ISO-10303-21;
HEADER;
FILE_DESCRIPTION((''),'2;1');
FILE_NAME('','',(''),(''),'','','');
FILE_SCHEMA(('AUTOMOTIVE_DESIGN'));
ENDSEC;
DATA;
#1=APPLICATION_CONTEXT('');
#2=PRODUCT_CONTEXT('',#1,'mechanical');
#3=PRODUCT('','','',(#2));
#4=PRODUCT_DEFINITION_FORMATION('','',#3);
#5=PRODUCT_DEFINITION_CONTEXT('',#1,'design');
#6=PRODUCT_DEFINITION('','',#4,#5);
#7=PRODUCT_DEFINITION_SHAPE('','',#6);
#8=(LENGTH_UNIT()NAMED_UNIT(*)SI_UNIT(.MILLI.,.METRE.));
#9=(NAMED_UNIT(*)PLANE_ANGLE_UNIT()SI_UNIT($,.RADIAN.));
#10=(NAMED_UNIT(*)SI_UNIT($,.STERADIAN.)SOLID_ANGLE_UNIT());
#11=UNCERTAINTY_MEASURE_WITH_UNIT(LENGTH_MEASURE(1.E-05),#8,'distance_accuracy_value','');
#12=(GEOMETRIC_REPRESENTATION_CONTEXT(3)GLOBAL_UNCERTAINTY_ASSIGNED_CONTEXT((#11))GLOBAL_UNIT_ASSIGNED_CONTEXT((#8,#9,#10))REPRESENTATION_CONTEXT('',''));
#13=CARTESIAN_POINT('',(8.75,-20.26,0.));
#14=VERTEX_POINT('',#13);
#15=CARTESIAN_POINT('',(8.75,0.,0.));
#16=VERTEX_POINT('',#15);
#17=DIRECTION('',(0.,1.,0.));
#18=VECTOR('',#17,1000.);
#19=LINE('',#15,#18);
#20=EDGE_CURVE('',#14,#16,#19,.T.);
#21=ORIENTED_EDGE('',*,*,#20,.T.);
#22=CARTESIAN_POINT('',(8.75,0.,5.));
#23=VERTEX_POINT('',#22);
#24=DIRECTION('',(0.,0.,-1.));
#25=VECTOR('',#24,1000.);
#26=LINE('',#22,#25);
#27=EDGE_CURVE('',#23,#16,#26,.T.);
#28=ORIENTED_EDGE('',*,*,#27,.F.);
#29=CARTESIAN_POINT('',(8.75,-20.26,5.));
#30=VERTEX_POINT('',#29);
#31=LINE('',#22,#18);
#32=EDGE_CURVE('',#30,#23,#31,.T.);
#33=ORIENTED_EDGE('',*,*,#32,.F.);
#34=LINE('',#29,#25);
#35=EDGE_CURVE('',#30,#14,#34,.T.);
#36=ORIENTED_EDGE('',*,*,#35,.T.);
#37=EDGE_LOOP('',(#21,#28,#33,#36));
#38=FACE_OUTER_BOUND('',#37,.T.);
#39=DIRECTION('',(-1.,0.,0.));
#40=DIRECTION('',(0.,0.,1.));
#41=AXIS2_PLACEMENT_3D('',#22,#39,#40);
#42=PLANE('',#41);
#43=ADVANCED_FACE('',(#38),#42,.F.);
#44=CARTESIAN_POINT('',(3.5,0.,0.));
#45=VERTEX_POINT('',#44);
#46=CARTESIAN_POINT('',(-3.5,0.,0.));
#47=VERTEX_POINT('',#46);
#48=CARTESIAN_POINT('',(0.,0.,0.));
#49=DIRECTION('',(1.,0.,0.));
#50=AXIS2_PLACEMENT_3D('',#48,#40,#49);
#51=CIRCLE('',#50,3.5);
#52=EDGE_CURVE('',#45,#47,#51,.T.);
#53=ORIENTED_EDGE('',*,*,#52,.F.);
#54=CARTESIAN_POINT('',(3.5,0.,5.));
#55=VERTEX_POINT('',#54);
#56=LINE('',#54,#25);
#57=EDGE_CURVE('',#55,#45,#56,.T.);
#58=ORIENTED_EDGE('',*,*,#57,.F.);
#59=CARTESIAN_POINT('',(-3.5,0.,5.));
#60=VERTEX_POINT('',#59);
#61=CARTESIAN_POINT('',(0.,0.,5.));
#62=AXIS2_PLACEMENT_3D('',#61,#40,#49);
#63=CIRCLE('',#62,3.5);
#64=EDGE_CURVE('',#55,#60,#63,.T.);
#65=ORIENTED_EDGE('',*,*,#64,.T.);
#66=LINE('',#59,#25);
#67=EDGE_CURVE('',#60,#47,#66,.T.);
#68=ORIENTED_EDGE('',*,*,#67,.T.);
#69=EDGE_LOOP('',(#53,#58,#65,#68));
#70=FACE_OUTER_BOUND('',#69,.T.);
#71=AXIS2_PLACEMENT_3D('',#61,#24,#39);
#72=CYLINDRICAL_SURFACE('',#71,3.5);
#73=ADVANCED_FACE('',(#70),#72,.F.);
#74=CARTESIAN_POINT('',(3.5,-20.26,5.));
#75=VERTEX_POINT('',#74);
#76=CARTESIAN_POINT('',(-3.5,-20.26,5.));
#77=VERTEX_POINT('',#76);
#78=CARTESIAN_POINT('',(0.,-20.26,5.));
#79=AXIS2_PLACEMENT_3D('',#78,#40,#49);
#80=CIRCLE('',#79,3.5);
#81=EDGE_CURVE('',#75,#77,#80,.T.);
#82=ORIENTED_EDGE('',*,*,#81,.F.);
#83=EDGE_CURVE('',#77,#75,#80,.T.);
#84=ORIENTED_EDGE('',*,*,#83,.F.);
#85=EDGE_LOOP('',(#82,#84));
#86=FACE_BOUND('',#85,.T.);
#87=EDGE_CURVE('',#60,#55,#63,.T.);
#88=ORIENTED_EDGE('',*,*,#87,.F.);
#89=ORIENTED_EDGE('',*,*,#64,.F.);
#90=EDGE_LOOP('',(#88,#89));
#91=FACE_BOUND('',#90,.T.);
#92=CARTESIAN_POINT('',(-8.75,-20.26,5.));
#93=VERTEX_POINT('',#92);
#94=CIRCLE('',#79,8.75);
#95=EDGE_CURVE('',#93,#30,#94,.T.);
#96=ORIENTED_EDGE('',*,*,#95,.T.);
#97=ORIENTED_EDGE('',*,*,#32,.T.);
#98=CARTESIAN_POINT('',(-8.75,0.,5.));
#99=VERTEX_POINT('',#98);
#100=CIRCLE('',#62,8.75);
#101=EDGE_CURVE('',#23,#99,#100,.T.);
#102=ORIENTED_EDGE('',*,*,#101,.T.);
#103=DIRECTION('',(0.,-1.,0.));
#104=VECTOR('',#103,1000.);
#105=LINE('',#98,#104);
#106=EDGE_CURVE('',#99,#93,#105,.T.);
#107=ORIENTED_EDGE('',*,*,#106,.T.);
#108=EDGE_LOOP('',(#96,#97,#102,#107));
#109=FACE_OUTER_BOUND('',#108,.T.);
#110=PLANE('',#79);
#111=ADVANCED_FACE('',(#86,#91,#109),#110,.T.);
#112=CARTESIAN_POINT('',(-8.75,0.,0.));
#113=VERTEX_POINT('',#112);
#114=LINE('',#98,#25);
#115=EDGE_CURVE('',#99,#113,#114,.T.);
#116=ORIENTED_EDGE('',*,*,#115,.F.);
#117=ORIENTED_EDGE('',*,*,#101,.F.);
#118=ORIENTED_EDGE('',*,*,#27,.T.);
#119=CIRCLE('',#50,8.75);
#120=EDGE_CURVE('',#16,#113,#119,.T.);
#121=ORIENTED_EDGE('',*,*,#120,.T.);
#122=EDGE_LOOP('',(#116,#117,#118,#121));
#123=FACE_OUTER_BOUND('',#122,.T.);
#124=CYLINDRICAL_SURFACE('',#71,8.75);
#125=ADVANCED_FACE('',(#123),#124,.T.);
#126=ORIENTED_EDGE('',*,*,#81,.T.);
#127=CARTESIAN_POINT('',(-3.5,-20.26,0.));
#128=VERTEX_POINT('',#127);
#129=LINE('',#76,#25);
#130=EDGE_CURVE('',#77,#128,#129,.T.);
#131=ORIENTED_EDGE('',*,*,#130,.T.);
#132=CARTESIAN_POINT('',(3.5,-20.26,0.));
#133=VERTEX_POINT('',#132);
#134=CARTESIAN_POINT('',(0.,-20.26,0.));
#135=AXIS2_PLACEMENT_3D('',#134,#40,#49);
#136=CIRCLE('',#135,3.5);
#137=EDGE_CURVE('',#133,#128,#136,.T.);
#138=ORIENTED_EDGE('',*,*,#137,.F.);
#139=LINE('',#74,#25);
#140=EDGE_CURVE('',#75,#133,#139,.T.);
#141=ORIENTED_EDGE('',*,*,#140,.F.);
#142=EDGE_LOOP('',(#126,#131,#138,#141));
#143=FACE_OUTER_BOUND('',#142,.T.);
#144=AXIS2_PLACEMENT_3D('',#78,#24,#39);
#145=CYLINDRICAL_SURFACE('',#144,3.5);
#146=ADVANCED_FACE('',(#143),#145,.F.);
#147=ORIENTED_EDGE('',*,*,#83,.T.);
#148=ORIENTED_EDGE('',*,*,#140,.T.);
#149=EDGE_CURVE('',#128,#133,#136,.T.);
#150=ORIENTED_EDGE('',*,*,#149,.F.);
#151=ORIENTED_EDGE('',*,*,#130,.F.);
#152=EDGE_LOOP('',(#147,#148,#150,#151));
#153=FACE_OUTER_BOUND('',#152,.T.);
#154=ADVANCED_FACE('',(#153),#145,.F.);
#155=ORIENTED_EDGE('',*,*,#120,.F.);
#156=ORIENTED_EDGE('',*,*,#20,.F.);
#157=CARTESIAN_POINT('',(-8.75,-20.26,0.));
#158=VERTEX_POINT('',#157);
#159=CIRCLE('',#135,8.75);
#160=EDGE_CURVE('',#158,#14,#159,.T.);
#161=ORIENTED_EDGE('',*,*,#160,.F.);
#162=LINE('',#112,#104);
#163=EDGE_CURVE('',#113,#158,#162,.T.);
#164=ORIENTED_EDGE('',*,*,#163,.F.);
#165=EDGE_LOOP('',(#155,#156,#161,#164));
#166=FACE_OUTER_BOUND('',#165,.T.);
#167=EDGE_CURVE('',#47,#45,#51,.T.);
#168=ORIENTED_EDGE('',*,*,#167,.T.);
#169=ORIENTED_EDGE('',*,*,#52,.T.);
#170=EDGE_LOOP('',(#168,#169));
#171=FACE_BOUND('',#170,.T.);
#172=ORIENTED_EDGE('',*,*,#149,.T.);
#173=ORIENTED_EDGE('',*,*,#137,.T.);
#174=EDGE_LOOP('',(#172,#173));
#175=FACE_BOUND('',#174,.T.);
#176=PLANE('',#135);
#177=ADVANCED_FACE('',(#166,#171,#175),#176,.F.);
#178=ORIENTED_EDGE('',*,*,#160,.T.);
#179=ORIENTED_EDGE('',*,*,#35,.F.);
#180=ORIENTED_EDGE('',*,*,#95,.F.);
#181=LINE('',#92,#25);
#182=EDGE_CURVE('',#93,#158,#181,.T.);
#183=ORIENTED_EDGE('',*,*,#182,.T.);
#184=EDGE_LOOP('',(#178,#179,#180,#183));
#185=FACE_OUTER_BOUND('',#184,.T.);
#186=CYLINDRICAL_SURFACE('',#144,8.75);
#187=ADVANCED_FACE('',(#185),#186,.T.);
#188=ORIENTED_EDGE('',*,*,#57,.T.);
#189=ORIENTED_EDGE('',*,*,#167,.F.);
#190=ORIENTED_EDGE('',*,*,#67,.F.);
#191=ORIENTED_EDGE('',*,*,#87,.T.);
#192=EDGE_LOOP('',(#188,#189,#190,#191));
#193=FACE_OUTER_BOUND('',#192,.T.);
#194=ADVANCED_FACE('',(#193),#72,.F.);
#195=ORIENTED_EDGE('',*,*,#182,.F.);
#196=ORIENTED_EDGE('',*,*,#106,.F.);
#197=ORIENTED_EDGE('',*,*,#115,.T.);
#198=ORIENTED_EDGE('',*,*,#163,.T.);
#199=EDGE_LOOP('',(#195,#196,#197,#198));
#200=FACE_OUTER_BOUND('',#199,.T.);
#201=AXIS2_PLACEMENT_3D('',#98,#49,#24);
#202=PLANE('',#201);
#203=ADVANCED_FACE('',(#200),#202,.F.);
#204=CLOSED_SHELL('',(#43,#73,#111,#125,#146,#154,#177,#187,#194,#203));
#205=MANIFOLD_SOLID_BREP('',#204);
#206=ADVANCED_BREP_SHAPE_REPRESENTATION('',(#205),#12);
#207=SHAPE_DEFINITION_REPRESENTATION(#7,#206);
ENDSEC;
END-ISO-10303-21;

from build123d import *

# Parameters (mm, degrees)
SKETCH1_R           = 3.5
BOSS_EXTRUDE1_DEPTH = 5


with BuildPart() as part:
    # Sketch1 → Boss-Extrude1 (new body)
    with BuildSketch(Plane.XY):
        with BuildLine():
            Line((-8.75, 0), (-8.75, -20.26))
            ThreePointArc((-8.75, -20.26), (0, -29.01), (8.75, -20.26))
            Line((8.75, -20.26), (8.75, 0))
            ThreePointArc((8.75, 0), (0, 8.75), (-8.75, 0))
        make_face()
        Circle(SKETCH1_R, mode=Mode.SUBTRACT)
        with Locations((0, -20.26)):
            Circle(SKETCH1_R, mode=Mode.SUBTRACT)
    extrude(amount=BOSS_EXTRUDE1_DEPTH)


solid = part.part
